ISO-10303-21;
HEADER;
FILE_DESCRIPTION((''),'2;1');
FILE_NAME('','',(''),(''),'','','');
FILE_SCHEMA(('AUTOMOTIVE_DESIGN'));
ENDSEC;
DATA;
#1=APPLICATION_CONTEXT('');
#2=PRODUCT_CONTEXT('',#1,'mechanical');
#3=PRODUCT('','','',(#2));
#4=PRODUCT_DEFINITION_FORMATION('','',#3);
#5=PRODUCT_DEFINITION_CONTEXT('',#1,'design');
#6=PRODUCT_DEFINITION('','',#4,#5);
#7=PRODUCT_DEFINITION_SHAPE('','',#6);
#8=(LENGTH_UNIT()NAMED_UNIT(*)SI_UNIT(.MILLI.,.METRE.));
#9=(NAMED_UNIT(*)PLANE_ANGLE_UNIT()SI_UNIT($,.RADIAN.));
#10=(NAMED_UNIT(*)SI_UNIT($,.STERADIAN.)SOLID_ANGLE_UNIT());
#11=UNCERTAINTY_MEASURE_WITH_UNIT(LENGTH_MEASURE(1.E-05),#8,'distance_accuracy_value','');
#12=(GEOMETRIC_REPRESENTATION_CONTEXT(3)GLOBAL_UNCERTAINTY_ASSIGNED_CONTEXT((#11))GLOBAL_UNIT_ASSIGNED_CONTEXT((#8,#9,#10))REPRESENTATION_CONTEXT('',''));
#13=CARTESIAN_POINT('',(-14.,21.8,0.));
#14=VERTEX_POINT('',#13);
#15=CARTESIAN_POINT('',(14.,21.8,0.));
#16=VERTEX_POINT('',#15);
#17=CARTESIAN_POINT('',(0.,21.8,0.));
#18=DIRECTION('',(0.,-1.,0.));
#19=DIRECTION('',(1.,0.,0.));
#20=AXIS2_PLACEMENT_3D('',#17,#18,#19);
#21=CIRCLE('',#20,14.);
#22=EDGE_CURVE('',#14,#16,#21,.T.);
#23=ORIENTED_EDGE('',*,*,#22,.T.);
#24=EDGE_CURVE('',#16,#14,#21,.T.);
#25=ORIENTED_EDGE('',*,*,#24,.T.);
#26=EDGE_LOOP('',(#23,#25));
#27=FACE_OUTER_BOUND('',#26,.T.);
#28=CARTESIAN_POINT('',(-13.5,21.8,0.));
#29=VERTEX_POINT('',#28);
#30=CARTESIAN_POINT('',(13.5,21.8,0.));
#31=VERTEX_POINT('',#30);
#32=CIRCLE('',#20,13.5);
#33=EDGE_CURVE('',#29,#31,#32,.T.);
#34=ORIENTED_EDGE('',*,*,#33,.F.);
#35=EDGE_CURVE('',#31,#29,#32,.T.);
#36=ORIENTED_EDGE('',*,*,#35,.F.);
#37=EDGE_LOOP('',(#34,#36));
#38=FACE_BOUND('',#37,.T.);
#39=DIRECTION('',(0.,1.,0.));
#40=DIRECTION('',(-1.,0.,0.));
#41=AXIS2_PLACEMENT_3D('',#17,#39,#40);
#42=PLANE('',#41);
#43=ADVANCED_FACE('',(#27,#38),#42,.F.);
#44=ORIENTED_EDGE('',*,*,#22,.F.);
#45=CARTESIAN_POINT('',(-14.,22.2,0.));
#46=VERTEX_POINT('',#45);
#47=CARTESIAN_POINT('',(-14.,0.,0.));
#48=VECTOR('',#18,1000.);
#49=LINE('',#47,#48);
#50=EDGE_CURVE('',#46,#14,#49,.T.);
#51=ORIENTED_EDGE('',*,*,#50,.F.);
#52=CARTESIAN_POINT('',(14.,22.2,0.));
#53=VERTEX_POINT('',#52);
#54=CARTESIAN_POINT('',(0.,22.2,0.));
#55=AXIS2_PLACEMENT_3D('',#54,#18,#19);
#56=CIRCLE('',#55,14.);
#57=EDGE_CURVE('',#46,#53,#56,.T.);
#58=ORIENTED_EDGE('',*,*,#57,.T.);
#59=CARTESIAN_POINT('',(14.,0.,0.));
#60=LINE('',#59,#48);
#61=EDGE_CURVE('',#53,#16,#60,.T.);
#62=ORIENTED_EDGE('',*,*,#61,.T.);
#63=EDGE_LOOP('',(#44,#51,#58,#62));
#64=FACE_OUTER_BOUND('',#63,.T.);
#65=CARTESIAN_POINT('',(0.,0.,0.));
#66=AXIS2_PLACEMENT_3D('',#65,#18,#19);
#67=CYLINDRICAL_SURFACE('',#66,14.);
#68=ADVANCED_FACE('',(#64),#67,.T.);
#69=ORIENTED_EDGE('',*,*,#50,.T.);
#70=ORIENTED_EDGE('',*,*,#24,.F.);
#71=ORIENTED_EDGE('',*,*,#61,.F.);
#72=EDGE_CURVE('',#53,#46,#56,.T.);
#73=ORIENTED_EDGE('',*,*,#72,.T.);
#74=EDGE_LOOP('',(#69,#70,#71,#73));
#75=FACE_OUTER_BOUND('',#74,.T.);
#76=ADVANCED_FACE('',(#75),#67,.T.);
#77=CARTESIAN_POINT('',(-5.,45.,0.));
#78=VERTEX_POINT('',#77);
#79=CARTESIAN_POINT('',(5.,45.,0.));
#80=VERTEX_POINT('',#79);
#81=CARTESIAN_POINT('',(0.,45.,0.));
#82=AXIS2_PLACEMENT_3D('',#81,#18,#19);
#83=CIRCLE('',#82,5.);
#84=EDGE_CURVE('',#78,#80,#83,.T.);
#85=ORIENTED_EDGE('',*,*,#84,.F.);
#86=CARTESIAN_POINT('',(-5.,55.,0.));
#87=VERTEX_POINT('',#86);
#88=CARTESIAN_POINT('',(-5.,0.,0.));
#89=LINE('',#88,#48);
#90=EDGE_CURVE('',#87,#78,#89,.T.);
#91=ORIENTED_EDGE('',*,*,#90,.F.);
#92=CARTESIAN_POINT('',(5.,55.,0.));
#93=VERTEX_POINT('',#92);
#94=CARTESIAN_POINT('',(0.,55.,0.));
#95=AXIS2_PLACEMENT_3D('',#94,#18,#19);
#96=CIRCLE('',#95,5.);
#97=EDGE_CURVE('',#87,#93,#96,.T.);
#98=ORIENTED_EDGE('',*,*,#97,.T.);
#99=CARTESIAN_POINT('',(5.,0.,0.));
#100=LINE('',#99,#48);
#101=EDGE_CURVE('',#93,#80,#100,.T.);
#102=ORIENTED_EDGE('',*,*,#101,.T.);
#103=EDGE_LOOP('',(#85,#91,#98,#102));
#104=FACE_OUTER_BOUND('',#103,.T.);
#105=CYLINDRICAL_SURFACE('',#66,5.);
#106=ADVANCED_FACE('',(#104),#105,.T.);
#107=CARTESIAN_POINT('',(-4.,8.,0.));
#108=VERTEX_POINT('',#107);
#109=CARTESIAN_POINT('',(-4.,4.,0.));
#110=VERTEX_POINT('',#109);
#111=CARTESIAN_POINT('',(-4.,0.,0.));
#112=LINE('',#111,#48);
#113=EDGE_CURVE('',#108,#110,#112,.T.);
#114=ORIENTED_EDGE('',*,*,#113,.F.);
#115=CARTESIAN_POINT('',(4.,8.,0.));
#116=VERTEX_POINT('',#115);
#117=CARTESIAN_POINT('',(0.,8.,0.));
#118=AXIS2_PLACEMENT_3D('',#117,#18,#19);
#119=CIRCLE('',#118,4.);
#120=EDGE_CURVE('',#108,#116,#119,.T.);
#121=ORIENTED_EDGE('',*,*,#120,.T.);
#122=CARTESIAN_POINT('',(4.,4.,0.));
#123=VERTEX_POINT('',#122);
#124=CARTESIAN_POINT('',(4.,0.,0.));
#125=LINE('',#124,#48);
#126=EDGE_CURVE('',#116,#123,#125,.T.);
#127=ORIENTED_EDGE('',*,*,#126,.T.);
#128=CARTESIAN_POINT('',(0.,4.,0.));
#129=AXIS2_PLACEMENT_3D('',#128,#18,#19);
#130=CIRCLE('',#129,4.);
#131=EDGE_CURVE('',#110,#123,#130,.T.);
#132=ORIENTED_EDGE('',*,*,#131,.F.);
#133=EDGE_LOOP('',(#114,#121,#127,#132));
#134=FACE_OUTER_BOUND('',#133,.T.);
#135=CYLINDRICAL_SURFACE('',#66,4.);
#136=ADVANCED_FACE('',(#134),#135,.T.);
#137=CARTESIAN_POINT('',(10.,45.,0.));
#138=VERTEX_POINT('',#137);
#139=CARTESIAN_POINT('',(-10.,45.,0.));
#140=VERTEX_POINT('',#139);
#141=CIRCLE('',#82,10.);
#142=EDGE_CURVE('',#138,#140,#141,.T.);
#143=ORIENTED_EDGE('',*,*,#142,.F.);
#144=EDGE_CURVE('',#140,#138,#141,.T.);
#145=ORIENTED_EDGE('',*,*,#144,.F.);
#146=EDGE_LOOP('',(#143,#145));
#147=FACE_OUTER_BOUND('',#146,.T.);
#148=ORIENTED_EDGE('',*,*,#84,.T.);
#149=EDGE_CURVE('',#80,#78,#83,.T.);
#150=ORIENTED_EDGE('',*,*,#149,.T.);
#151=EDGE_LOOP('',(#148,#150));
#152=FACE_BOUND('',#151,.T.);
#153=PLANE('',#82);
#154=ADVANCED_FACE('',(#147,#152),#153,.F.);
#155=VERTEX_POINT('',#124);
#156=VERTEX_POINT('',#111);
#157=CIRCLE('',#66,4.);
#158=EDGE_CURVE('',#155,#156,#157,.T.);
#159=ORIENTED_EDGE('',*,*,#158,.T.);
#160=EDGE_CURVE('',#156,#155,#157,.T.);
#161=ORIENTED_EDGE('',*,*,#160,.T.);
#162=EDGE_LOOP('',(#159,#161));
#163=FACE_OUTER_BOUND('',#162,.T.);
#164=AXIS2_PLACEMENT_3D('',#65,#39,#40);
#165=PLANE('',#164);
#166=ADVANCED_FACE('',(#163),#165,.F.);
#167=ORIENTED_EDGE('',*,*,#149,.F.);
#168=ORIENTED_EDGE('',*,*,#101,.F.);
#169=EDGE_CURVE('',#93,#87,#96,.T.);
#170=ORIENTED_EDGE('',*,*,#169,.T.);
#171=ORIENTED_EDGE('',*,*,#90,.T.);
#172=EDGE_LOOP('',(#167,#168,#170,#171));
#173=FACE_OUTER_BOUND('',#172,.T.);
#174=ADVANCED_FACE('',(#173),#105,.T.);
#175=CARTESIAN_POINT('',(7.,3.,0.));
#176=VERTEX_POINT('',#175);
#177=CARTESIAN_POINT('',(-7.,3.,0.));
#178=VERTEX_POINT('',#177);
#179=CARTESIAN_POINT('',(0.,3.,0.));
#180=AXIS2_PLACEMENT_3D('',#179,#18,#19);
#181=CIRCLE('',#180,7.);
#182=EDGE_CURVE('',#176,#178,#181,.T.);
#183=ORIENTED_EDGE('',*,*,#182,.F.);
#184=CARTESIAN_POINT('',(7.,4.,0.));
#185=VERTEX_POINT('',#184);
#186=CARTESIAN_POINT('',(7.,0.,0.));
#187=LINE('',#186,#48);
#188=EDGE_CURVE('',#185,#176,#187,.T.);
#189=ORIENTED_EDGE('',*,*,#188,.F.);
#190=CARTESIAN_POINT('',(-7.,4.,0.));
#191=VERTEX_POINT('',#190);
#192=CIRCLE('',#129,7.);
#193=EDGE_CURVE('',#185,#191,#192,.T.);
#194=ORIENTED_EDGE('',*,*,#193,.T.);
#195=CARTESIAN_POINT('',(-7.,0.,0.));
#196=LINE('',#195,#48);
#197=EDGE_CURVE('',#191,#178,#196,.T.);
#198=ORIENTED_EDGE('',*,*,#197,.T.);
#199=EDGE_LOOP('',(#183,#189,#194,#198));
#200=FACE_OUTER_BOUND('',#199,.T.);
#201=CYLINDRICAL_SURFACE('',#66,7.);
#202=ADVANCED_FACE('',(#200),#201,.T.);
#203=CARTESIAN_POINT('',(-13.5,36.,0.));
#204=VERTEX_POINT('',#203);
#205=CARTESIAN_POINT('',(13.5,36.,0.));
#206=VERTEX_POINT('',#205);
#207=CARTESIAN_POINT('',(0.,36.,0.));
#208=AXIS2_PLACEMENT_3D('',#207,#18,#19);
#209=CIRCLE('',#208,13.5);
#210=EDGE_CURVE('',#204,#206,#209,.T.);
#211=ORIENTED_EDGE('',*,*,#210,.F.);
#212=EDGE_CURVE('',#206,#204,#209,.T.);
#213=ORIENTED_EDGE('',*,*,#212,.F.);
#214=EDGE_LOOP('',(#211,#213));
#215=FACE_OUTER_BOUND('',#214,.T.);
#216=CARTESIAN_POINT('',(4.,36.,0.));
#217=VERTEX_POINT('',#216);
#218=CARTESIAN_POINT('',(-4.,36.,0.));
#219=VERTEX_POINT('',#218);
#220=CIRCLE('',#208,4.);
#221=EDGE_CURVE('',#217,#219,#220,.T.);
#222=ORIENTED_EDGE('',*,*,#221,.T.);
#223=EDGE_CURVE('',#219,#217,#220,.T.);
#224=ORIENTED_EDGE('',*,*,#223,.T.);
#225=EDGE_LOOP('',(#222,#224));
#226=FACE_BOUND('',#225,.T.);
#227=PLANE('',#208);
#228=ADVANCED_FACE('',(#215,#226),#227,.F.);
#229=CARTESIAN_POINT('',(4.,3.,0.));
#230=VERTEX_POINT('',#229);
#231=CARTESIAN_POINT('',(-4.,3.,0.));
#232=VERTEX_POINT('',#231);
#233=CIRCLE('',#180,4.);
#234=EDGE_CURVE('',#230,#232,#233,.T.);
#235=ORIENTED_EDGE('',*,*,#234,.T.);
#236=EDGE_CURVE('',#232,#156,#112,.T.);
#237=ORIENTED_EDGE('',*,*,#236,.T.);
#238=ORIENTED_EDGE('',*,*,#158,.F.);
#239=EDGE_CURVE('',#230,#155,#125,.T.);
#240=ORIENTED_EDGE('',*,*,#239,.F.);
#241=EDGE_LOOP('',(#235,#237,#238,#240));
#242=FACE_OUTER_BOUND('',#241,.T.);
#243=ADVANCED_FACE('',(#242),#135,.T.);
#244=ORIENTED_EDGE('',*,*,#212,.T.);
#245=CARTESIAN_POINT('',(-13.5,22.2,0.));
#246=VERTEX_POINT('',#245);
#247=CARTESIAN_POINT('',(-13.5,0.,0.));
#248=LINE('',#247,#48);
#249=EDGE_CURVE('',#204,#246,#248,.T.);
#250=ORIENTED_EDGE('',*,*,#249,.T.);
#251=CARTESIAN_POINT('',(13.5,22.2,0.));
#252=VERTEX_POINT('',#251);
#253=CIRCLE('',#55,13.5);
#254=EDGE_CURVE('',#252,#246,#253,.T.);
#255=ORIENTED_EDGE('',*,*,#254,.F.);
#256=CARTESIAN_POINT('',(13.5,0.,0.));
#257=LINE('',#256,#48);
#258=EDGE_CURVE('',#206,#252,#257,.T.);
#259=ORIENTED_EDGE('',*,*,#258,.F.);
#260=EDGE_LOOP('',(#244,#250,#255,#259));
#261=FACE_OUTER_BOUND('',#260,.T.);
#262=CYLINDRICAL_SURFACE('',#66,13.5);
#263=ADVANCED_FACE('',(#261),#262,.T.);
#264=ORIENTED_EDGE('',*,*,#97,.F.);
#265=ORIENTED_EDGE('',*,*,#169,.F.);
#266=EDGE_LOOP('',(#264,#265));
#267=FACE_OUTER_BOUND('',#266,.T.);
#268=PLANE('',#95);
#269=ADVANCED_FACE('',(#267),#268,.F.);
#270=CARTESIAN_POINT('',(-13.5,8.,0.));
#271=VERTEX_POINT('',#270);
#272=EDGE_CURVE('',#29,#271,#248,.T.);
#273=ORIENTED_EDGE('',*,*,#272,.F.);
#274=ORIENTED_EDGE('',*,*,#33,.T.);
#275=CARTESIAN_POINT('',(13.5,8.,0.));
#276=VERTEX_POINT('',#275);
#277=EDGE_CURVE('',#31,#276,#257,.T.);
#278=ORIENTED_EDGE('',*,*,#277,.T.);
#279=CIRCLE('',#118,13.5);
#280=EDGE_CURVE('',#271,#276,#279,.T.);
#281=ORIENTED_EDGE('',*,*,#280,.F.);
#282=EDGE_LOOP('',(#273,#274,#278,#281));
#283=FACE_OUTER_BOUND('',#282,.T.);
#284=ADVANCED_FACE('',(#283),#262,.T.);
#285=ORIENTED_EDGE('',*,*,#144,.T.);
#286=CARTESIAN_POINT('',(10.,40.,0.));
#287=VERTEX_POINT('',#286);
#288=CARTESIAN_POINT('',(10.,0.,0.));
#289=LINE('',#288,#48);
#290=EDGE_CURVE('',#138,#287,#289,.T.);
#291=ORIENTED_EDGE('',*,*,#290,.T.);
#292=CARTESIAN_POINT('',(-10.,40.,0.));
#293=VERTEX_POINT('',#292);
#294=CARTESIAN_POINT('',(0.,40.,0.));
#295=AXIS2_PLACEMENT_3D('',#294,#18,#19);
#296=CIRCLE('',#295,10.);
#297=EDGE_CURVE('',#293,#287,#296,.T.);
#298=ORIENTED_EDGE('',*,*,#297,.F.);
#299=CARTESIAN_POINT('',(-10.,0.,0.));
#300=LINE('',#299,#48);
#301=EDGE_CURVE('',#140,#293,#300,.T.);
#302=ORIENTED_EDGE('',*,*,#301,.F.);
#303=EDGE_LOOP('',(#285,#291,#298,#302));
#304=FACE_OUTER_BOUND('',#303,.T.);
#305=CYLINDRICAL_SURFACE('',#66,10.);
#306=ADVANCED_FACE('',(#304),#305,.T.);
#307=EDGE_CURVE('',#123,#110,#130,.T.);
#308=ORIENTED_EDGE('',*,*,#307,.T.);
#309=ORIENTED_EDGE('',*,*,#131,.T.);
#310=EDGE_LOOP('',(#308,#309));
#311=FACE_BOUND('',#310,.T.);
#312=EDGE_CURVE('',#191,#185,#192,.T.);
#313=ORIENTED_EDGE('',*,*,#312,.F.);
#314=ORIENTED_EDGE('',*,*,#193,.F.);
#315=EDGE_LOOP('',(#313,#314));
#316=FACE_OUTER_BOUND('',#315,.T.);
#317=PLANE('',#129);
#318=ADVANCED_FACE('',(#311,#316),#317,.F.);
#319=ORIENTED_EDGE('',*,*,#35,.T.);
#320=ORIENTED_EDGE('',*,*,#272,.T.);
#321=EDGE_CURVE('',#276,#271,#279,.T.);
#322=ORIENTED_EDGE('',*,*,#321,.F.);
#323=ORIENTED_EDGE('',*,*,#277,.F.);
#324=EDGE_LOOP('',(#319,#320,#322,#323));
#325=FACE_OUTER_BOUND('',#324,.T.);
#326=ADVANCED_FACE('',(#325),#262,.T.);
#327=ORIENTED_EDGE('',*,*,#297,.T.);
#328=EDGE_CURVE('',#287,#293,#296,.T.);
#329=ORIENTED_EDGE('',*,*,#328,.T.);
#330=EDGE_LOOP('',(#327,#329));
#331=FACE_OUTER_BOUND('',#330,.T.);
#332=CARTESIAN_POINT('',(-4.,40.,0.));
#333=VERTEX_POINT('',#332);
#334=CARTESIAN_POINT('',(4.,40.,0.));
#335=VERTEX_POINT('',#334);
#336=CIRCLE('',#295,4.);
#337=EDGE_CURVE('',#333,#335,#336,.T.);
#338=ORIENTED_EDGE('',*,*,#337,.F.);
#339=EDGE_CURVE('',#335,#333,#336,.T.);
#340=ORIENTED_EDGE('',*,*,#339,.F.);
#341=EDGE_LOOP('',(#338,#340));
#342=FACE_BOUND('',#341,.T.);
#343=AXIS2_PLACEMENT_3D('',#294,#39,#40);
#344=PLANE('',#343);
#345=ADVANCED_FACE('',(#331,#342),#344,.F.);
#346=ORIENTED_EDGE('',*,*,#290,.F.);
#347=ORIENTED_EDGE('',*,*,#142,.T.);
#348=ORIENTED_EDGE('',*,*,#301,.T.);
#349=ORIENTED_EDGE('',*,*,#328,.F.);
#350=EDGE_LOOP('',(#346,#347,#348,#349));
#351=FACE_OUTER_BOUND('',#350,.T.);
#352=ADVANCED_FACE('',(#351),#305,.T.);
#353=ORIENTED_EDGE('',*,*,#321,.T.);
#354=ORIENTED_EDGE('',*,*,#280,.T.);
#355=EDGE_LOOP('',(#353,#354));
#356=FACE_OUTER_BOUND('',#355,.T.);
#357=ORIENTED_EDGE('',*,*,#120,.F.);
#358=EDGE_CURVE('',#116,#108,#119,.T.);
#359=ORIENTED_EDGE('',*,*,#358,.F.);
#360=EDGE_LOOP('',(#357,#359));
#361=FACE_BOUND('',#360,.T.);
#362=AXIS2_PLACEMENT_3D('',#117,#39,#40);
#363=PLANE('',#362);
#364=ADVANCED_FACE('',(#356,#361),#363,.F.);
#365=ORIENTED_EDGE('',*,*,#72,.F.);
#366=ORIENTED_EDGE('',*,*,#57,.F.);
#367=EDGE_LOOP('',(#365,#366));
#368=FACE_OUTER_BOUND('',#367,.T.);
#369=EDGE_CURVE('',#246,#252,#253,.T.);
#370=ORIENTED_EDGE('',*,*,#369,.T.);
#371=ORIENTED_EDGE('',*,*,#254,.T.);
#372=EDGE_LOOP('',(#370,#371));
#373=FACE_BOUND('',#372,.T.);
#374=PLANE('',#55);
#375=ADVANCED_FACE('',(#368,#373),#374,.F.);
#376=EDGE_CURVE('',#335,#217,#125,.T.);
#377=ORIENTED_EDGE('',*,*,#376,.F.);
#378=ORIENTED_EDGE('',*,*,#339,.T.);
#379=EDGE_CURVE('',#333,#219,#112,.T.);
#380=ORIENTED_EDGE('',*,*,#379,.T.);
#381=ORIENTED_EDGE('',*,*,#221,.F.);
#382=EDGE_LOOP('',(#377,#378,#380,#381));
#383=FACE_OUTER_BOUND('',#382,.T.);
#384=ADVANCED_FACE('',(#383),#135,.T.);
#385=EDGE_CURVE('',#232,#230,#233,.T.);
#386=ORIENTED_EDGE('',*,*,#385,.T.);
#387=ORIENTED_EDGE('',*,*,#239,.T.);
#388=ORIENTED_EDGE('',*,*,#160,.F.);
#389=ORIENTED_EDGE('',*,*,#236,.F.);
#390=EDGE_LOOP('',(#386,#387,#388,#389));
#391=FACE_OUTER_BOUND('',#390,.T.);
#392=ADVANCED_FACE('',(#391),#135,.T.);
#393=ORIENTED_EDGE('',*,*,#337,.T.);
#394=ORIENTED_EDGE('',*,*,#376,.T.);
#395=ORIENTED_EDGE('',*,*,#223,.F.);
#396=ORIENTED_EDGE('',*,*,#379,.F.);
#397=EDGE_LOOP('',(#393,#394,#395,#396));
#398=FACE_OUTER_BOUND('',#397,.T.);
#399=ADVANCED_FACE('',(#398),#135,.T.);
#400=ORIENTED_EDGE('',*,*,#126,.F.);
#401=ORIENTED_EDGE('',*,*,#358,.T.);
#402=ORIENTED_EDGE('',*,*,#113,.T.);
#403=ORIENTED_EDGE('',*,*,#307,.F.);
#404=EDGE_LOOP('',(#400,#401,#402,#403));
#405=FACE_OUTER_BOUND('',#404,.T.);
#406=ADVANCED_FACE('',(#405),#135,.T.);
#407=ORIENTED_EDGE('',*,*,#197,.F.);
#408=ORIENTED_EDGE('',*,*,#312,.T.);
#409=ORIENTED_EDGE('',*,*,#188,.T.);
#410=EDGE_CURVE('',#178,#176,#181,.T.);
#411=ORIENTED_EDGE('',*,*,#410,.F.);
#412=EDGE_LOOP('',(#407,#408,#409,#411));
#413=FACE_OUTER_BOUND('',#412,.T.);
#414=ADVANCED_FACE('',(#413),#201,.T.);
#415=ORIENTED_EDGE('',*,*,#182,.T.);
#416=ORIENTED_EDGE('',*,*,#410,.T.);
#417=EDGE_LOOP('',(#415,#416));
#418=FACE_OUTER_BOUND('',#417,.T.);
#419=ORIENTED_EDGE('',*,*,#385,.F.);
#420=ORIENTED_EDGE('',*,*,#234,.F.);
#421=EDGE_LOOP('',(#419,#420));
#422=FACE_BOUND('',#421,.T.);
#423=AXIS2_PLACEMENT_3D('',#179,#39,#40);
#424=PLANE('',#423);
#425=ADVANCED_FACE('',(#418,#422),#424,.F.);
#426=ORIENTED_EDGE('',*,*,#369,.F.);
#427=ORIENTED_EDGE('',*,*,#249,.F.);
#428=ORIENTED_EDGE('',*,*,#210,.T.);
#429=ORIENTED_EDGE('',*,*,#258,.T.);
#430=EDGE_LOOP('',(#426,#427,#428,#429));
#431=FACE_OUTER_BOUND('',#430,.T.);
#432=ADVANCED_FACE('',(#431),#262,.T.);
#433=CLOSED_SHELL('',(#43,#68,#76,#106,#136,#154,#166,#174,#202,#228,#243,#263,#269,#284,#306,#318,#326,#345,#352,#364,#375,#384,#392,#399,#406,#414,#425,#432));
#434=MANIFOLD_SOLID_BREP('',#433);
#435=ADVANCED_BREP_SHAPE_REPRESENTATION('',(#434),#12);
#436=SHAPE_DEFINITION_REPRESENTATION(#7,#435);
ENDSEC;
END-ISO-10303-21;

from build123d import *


with BuildPart() as part:
    # Sketch1 → Revolve1 (revolve)
    with BuildSketch(Plane.XY, mode=Mode.PRIVATE) as revolve1_sk:
        Polygon((0, 0), (0, 55), (-5, 55), (-5, 45), (-10, 45), (-10, 40), (-4, 40), (-4, 36), (-13.5, 36), (-13.5, 22.2), (-14, 22.2), (-14, 21.8), (-13.5, 21.8), (-13.5, 8), (-4, 8), (-4, 4), (-7, 4), (-7, 3), (-4, 3), (-4, 0), align=None)
    revolve(revolve1_sk.sketch.rotate(Axis((0, 0, 0), (0, 1, 0)), 180), axis=Axis((0, 0, 0), (0, 1, 0)))


solid = part.part
